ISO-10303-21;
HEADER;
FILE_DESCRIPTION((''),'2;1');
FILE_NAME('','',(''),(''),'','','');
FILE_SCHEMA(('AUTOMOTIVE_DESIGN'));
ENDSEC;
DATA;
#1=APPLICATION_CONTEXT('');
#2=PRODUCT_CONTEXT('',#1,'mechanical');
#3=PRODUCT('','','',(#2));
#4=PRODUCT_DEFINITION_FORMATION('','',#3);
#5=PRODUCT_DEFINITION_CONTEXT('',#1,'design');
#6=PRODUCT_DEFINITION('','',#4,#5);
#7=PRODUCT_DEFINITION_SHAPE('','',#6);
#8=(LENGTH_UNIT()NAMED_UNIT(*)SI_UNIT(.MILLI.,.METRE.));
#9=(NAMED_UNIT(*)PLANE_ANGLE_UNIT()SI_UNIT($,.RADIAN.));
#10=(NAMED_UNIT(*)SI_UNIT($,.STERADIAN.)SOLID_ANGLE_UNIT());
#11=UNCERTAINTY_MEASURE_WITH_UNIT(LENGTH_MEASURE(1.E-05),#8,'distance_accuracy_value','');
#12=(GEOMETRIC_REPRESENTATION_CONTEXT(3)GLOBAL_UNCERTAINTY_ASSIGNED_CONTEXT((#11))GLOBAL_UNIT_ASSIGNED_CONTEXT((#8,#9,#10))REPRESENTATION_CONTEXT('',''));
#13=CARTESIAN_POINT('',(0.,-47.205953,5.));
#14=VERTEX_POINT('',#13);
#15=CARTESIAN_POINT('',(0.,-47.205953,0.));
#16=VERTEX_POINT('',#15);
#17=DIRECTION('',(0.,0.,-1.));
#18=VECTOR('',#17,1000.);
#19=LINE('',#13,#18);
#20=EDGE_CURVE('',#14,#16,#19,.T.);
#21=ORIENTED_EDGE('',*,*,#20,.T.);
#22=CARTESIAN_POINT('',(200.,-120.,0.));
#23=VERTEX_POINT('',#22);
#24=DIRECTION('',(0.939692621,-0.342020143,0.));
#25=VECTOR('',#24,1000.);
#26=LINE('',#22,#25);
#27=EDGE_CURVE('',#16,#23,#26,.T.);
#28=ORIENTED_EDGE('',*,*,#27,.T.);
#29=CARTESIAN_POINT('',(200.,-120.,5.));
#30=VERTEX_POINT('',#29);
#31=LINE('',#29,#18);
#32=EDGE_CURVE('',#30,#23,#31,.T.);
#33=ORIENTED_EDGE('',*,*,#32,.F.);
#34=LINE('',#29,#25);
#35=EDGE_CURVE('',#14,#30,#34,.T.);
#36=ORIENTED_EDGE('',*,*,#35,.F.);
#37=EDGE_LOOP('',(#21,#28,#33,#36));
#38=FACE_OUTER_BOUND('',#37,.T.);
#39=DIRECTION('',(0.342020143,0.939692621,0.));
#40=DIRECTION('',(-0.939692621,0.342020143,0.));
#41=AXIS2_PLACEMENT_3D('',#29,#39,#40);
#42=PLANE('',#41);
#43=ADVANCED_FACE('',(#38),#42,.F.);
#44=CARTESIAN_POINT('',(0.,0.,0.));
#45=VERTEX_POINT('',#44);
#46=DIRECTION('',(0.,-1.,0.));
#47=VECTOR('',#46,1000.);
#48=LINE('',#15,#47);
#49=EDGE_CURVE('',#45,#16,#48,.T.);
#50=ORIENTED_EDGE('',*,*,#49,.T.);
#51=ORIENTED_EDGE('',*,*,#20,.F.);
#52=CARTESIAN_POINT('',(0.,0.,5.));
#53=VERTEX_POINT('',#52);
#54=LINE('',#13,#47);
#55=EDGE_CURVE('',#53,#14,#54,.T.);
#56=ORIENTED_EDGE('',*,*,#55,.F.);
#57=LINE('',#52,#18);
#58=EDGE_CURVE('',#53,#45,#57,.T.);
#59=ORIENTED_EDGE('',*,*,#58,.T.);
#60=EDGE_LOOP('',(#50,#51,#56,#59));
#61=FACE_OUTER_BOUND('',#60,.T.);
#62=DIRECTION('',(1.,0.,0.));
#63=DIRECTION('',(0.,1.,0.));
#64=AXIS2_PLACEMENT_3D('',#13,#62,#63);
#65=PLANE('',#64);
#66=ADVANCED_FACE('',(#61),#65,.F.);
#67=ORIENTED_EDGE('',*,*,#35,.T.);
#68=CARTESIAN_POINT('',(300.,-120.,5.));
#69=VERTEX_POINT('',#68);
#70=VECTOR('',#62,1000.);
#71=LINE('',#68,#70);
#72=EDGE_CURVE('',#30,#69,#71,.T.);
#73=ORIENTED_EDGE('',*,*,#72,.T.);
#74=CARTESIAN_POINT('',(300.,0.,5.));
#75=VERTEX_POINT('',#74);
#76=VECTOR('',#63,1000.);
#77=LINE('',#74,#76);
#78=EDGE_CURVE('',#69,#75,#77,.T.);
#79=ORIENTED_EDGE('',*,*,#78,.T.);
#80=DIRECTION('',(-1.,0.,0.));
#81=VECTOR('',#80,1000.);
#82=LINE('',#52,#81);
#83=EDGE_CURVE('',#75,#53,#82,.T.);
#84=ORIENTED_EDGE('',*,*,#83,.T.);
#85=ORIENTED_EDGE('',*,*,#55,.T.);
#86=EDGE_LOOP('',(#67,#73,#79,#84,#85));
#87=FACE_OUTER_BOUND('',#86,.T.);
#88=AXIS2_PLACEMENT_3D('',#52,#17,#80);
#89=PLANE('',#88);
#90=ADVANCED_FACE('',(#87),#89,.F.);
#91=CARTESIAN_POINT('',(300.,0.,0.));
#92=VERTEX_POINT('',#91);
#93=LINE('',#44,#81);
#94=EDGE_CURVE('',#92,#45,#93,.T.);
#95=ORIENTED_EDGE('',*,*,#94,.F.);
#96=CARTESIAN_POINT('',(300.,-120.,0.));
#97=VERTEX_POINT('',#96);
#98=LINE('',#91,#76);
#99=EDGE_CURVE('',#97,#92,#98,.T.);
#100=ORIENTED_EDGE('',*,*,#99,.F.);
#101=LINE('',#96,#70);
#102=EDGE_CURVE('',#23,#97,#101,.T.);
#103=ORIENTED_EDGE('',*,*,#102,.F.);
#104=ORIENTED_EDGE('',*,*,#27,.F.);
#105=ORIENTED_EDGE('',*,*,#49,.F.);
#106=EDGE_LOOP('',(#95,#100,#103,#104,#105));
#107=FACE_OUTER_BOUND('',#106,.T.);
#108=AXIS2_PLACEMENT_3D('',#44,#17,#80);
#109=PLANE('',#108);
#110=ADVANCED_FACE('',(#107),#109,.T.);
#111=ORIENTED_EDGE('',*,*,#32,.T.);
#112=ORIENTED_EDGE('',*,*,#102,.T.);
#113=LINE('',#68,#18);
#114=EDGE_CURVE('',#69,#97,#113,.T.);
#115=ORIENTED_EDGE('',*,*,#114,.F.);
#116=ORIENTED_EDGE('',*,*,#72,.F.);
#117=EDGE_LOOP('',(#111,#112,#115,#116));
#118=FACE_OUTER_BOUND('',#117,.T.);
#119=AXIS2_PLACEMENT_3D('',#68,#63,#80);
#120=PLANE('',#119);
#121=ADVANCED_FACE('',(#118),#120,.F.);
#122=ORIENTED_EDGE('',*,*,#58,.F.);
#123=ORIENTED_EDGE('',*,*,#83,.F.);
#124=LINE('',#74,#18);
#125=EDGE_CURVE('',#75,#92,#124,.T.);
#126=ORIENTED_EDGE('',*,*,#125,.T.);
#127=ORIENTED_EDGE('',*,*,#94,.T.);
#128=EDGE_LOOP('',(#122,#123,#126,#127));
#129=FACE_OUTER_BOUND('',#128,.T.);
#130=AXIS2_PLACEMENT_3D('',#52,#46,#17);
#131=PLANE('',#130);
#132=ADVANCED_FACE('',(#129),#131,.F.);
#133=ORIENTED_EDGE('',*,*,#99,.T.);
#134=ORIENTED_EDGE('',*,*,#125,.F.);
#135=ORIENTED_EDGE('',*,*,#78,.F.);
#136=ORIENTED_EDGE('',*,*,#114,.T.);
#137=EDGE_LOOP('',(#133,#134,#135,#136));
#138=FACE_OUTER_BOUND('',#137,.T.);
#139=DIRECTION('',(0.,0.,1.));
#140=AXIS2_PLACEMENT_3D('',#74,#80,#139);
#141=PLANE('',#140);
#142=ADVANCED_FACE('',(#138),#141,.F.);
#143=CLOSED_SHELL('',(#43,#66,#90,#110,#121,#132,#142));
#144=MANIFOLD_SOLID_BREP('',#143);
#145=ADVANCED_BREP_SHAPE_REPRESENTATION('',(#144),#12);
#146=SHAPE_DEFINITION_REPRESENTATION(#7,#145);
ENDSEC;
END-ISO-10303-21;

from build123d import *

# Parameters (mm, degrees)
EXTRUDE_1_DEPTH = 5


with BuildPart() as part:
    # 草图1 → 凸台-拉伸1 (new body)
    with BuildSketch(Plane.XY):
        Polygon((0, 0), (300, 0), (300, -120), (200, -120), (0, -47.205953147), align=None)
    extrude(amount=EXTRUDE_1_DEPTH)


solid = part.part
